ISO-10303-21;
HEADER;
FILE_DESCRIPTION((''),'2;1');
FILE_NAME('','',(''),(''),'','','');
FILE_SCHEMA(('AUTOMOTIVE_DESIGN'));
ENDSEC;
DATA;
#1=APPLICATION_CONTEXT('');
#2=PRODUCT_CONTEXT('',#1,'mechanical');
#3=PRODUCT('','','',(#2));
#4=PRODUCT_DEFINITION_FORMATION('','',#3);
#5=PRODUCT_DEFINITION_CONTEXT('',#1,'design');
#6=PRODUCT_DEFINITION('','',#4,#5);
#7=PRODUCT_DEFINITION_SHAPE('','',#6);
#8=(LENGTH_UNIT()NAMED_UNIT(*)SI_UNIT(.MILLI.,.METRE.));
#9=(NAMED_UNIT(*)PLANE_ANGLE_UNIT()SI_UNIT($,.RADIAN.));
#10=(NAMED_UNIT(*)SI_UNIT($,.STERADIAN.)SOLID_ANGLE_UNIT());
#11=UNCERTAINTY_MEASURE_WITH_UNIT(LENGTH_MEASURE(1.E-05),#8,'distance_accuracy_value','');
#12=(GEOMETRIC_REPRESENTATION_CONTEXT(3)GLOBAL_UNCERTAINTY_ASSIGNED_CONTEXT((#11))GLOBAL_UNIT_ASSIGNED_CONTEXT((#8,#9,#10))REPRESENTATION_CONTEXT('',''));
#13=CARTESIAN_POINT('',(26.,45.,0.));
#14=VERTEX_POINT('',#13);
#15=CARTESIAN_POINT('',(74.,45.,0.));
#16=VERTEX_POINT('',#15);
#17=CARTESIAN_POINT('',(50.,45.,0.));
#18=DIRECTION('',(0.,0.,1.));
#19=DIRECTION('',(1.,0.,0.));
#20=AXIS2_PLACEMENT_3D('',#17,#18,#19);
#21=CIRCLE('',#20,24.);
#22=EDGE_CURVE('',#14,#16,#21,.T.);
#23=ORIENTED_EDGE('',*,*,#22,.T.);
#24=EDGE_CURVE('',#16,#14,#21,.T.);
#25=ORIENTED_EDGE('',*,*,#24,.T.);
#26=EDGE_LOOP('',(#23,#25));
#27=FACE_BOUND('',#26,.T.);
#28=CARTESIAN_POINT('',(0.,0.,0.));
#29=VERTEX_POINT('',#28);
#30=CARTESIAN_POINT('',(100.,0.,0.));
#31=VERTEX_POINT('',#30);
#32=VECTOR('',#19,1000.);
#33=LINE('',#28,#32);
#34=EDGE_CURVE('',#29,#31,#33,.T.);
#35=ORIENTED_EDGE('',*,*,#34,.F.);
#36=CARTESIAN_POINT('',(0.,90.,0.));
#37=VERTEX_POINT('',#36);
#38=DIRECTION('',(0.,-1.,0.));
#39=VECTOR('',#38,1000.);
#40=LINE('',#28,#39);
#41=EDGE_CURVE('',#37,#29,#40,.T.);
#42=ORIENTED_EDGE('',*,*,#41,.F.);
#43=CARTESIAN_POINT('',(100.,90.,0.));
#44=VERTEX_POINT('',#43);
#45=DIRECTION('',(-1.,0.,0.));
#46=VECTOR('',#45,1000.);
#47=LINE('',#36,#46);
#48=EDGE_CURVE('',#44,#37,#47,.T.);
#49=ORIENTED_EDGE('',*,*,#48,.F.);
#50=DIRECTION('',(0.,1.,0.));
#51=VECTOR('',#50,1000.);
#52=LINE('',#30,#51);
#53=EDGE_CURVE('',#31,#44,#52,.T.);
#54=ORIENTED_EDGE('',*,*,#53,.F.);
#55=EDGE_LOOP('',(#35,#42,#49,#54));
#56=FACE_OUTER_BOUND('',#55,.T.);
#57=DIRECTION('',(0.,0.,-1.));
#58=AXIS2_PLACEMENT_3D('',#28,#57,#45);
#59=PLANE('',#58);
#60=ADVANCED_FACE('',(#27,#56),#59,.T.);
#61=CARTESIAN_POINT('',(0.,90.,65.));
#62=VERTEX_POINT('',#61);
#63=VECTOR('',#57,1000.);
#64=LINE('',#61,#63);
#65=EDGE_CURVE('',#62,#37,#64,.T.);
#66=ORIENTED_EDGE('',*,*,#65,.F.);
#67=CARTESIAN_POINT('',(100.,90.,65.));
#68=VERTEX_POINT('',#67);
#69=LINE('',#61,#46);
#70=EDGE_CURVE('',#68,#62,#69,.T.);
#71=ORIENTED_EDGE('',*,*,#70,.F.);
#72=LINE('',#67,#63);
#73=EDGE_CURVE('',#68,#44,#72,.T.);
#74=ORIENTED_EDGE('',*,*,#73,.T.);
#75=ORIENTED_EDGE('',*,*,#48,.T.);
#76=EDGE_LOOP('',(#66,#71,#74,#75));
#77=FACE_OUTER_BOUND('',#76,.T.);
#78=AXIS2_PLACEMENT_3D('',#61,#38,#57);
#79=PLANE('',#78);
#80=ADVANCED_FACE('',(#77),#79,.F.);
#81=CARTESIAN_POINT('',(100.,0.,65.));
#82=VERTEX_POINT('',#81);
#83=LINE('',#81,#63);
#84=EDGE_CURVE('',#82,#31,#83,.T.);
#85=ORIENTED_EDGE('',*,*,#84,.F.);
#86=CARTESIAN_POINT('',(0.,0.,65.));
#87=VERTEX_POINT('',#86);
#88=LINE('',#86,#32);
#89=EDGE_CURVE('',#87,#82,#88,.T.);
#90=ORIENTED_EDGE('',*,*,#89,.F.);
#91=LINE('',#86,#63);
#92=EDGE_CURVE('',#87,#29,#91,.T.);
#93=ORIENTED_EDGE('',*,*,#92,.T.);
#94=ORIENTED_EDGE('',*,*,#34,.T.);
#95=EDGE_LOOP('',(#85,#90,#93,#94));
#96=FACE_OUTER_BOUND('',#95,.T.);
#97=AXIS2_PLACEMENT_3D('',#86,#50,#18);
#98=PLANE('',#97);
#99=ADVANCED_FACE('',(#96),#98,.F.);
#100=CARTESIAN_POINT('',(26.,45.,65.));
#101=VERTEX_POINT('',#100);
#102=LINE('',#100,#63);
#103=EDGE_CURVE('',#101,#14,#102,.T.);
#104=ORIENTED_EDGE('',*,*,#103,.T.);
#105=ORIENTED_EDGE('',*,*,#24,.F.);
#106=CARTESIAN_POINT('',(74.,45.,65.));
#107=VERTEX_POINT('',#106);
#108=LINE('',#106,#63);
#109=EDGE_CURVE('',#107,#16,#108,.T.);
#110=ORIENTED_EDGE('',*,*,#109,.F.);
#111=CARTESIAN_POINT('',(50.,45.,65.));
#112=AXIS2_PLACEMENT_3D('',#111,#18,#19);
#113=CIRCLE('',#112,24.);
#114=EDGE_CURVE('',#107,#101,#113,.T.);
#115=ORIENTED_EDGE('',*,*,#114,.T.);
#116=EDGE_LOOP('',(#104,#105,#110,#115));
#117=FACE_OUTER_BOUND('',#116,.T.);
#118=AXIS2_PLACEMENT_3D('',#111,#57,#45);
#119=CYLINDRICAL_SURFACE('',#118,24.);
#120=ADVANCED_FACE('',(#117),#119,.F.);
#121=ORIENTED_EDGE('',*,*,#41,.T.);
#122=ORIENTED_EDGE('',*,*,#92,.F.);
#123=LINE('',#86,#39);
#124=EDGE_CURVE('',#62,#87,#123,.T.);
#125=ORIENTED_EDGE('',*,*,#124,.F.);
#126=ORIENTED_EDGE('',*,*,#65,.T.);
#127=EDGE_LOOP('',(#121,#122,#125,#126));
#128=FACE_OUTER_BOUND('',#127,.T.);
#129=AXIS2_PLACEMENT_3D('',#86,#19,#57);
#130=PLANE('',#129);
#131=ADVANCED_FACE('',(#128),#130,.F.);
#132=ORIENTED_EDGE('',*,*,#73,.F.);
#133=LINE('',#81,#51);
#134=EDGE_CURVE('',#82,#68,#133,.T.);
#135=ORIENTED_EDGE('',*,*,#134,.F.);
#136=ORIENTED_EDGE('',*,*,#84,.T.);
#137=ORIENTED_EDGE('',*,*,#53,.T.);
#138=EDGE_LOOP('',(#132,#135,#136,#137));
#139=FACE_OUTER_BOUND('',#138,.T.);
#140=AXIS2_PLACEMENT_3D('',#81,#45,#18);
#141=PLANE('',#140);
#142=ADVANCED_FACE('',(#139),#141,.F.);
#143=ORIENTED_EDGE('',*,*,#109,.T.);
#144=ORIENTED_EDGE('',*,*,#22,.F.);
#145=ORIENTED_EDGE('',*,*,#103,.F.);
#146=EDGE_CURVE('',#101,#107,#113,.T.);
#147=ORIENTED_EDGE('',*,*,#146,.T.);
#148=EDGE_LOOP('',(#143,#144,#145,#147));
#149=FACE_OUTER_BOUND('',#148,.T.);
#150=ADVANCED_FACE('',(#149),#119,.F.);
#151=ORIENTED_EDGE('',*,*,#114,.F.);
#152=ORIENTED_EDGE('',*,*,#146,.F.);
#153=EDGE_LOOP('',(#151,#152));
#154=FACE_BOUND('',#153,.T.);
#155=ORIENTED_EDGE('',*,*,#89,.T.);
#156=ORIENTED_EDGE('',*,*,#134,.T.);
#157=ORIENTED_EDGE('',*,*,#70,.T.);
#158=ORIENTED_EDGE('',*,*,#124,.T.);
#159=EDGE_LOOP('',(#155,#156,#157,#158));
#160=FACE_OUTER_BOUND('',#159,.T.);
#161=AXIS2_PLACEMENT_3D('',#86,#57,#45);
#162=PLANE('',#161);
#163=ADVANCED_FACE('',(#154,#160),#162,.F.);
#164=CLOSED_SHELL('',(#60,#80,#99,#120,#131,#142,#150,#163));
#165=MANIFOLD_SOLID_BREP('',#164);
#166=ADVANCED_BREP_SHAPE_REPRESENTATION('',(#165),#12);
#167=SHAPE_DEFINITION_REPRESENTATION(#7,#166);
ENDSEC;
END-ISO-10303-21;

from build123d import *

# Parameters (mm, degrees)
SKETCH1_W           = 100
SKETCH1_H           = 90
SKETCH1_R           = 24
BOSS_EXTRUDE1_DEPTH = 65


with BuildPart() as part:
    # Sketch1 → Boss-Extrude1 (new body)
    with BuildSketch(Plane.XY):
        with Locations((50, 45)):
            Rectangle(SKETCH1_W, SKETCH1_H)
        with Locations((50, 45)):
            Circle(SKETCH1_R, mode=Mode.SUBTRACT)
    extrude(amount=BOSS_EXTRUDE1_DEPTH)


solid = part.part
